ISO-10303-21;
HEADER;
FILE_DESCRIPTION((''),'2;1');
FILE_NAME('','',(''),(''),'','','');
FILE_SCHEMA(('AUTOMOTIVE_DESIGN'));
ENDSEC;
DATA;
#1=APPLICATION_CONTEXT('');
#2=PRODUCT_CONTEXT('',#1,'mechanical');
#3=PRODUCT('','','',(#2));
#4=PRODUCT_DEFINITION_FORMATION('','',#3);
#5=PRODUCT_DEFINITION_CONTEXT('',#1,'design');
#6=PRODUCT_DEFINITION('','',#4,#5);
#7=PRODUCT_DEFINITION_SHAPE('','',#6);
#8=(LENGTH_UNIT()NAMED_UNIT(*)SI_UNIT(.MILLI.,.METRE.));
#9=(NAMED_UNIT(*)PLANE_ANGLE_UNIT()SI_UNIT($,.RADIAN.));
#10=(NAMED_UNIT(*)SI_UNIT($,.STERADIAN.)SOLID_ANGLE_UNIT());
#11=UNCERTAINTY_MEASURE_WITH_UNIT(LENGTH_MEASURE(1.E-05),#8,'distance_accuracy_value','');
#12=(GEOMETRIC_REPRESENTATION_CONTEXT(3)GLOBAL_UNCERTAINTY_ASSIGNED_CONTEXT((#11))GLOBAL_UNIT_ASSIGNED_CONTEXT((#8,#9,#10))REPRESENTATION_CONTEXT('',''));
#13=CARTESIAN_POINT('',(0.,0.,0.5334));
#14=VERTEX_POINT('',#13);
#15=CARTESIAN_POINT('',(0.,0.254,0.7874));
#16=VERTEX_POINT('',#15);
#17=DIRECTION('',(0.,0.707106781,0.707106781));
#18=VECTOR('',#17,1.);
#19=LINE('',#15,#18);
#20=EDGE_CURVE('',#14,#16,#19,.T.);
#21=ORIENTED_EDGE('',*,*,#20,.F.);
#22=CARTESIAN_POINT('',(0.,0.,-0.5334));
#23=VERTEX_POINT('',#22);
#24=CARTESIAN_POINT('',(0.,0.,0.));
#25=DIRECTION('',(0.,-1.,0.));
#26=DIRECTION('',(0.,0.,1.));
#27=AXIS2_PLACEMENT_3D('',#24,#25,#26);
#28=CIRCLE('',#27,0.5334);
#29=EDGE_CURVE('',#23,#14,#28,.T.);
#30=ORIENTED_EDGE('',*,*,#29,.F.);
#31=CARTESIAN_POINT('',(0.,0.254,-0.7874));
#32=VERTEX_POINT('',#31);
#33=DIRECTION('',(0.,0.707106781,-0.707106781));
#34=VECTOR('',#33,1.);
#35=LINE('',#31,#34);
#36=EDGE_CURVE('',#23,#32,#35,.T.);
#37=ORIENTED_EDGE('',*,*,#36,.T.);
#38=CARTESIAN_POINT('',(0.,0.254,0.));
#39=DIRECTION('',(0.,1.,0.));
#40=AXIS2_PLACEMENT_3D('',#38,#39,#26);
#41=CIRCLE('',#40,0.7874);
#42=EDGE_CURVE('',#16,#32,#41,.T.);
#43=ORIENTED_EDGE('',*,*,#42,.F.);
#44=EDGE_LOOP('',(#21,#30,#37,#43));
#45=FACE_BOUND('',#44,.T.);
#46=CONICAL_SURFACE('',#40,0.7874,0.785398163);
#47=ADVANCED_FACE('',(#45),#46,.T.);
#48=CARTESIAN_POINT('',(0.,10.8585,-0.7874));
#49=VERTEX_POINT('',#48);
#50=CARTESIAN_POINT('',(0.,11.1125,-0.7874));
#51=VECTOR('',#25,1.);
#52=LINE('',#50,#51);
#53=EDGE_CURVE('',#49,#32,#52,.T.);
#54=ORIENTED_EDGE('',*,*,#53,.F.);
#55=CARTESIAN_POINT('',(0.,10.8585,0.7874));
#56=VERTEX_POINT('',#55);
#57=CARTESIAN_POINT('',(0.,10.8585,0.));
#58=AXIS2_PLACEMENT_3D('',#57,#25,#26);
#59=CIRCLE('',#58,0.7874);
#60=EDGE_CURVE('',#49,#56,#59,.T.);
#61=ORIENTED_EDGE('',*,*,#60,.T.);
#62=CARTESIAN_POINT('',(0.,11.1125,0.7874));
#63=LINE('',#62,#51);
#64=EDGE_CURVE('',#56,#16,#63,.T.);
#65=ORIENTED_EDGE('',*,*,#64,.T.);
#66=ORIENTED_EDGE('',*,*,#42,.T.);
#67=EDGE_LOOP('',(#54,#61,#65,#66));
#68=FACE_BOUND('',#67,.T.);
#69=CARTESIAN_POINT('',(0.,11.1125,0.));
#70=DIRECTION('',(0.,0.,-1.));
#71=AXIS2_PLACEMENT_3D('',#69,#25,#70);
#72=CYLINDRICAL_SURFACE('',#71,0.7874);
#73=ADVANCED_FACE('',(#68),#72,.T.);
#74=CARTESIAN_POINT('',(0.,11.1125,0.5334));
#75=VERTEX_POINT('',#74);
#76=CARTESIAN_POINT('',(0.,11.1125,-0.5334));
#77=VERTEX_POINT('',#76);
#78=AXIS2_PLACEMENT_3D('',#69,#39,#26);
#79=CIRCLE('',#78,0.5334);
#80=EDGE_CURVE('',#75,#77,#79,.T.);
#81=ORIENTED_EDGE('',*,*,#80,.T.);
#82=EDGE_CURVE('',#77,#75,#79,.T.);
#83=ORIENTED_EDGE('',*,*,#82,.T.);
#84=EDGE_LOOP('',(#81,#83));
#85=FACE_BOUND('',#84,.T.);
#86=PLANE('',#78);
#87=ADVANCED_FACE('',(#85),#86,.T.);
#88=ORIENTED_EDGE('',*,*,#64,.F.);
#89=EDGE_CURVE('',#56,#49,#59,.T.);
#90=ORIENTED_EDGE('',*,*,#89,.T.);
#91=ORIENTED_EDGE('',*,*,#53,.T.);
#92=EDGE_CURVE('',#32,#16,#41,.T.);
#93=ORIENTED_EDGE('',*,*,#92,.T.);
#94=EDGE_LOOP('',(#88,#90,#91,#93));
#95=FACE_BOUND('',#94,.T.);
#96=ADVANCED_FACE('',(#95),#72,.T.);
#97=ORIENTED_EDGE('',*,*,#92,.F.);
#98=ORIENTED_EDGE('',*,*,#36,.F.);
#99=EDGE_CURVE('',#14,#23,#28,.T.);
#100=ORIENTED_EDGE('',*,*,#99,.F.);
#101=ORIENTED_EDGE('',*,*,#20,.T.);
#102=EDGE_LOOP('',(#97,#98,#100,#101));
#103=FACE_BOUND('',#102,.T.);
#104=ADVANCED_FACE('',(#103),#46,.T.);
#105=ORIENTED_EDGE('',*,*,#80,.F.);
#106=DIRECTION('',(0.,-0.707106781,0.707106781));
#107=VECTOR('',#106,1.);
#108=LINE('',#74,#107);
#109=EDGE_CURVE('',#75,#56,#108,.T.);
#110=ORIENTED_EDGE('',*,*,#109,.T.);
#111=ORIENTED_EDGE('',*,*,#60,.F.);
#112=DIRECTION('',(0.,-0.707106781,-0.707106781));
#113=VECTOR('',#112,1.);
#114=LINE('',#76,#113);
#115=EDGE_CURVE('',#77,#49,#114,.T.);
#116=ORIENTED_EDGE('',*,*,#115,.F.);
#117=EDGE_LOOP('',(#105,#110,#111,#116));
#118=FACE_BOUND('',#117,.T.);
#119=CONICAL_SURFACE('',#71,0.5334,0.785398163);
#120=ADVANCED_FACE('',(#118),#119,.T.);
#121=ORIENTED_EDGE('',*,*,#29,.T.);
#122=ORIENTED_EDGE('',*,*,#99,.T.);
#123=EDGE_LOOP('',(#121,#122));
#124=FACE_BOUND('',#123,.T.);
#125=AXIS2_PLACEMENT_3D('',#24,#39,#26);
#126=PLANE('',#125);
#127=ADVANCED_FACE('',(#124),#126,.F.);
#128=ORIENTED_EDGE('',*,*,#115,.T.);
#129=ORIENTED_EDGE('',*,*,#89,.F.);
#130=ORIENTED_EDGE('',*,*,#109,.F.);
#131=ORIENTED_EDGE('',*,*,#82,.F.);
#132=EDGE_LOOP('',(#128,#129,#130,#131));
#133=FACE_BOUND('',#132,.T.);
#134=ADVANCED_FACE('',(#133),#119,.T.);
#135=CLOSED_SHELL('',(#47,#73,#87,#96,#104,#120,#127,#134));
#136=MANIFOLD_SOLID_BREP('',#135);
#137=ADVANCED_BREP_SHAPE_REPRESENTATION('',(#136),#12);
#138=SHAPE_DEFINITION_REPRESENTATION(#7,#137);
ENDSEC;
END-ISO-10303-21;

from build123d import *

# Parameters (mm, degrees)
SKETCH1_R           = 0.7874
BOSS_EXTRUDE1_DEPTH = 11.1125
CHAMFER1_SIZE       = 0.254


with BuildPart() as part:
    # Sketch1 → Boss-Extrude1 (new body)
    with BuildSketch(Plane(origin=(0, 0, 0), x_dir=(1, 0, 0), z_dir=(0, 1, 0))):
        with Locations(Location((0, 0, 0), (0, 0, 270))):
            Circle(SKETCH1_R)
    extrude(amount=BOSS_EXTRUDE1_DEPTH)

    # Chamfer1
    chamfer1_edges = [part.edges().sort_by_distance(p)[0] for p in [
        (0, 0, -0.7874),
        (0, 11.1125, -0.7874),
    ]]
    chamfer(chamfer1_edges, length=CHAMFER1_SIZE)


solid = part.part
